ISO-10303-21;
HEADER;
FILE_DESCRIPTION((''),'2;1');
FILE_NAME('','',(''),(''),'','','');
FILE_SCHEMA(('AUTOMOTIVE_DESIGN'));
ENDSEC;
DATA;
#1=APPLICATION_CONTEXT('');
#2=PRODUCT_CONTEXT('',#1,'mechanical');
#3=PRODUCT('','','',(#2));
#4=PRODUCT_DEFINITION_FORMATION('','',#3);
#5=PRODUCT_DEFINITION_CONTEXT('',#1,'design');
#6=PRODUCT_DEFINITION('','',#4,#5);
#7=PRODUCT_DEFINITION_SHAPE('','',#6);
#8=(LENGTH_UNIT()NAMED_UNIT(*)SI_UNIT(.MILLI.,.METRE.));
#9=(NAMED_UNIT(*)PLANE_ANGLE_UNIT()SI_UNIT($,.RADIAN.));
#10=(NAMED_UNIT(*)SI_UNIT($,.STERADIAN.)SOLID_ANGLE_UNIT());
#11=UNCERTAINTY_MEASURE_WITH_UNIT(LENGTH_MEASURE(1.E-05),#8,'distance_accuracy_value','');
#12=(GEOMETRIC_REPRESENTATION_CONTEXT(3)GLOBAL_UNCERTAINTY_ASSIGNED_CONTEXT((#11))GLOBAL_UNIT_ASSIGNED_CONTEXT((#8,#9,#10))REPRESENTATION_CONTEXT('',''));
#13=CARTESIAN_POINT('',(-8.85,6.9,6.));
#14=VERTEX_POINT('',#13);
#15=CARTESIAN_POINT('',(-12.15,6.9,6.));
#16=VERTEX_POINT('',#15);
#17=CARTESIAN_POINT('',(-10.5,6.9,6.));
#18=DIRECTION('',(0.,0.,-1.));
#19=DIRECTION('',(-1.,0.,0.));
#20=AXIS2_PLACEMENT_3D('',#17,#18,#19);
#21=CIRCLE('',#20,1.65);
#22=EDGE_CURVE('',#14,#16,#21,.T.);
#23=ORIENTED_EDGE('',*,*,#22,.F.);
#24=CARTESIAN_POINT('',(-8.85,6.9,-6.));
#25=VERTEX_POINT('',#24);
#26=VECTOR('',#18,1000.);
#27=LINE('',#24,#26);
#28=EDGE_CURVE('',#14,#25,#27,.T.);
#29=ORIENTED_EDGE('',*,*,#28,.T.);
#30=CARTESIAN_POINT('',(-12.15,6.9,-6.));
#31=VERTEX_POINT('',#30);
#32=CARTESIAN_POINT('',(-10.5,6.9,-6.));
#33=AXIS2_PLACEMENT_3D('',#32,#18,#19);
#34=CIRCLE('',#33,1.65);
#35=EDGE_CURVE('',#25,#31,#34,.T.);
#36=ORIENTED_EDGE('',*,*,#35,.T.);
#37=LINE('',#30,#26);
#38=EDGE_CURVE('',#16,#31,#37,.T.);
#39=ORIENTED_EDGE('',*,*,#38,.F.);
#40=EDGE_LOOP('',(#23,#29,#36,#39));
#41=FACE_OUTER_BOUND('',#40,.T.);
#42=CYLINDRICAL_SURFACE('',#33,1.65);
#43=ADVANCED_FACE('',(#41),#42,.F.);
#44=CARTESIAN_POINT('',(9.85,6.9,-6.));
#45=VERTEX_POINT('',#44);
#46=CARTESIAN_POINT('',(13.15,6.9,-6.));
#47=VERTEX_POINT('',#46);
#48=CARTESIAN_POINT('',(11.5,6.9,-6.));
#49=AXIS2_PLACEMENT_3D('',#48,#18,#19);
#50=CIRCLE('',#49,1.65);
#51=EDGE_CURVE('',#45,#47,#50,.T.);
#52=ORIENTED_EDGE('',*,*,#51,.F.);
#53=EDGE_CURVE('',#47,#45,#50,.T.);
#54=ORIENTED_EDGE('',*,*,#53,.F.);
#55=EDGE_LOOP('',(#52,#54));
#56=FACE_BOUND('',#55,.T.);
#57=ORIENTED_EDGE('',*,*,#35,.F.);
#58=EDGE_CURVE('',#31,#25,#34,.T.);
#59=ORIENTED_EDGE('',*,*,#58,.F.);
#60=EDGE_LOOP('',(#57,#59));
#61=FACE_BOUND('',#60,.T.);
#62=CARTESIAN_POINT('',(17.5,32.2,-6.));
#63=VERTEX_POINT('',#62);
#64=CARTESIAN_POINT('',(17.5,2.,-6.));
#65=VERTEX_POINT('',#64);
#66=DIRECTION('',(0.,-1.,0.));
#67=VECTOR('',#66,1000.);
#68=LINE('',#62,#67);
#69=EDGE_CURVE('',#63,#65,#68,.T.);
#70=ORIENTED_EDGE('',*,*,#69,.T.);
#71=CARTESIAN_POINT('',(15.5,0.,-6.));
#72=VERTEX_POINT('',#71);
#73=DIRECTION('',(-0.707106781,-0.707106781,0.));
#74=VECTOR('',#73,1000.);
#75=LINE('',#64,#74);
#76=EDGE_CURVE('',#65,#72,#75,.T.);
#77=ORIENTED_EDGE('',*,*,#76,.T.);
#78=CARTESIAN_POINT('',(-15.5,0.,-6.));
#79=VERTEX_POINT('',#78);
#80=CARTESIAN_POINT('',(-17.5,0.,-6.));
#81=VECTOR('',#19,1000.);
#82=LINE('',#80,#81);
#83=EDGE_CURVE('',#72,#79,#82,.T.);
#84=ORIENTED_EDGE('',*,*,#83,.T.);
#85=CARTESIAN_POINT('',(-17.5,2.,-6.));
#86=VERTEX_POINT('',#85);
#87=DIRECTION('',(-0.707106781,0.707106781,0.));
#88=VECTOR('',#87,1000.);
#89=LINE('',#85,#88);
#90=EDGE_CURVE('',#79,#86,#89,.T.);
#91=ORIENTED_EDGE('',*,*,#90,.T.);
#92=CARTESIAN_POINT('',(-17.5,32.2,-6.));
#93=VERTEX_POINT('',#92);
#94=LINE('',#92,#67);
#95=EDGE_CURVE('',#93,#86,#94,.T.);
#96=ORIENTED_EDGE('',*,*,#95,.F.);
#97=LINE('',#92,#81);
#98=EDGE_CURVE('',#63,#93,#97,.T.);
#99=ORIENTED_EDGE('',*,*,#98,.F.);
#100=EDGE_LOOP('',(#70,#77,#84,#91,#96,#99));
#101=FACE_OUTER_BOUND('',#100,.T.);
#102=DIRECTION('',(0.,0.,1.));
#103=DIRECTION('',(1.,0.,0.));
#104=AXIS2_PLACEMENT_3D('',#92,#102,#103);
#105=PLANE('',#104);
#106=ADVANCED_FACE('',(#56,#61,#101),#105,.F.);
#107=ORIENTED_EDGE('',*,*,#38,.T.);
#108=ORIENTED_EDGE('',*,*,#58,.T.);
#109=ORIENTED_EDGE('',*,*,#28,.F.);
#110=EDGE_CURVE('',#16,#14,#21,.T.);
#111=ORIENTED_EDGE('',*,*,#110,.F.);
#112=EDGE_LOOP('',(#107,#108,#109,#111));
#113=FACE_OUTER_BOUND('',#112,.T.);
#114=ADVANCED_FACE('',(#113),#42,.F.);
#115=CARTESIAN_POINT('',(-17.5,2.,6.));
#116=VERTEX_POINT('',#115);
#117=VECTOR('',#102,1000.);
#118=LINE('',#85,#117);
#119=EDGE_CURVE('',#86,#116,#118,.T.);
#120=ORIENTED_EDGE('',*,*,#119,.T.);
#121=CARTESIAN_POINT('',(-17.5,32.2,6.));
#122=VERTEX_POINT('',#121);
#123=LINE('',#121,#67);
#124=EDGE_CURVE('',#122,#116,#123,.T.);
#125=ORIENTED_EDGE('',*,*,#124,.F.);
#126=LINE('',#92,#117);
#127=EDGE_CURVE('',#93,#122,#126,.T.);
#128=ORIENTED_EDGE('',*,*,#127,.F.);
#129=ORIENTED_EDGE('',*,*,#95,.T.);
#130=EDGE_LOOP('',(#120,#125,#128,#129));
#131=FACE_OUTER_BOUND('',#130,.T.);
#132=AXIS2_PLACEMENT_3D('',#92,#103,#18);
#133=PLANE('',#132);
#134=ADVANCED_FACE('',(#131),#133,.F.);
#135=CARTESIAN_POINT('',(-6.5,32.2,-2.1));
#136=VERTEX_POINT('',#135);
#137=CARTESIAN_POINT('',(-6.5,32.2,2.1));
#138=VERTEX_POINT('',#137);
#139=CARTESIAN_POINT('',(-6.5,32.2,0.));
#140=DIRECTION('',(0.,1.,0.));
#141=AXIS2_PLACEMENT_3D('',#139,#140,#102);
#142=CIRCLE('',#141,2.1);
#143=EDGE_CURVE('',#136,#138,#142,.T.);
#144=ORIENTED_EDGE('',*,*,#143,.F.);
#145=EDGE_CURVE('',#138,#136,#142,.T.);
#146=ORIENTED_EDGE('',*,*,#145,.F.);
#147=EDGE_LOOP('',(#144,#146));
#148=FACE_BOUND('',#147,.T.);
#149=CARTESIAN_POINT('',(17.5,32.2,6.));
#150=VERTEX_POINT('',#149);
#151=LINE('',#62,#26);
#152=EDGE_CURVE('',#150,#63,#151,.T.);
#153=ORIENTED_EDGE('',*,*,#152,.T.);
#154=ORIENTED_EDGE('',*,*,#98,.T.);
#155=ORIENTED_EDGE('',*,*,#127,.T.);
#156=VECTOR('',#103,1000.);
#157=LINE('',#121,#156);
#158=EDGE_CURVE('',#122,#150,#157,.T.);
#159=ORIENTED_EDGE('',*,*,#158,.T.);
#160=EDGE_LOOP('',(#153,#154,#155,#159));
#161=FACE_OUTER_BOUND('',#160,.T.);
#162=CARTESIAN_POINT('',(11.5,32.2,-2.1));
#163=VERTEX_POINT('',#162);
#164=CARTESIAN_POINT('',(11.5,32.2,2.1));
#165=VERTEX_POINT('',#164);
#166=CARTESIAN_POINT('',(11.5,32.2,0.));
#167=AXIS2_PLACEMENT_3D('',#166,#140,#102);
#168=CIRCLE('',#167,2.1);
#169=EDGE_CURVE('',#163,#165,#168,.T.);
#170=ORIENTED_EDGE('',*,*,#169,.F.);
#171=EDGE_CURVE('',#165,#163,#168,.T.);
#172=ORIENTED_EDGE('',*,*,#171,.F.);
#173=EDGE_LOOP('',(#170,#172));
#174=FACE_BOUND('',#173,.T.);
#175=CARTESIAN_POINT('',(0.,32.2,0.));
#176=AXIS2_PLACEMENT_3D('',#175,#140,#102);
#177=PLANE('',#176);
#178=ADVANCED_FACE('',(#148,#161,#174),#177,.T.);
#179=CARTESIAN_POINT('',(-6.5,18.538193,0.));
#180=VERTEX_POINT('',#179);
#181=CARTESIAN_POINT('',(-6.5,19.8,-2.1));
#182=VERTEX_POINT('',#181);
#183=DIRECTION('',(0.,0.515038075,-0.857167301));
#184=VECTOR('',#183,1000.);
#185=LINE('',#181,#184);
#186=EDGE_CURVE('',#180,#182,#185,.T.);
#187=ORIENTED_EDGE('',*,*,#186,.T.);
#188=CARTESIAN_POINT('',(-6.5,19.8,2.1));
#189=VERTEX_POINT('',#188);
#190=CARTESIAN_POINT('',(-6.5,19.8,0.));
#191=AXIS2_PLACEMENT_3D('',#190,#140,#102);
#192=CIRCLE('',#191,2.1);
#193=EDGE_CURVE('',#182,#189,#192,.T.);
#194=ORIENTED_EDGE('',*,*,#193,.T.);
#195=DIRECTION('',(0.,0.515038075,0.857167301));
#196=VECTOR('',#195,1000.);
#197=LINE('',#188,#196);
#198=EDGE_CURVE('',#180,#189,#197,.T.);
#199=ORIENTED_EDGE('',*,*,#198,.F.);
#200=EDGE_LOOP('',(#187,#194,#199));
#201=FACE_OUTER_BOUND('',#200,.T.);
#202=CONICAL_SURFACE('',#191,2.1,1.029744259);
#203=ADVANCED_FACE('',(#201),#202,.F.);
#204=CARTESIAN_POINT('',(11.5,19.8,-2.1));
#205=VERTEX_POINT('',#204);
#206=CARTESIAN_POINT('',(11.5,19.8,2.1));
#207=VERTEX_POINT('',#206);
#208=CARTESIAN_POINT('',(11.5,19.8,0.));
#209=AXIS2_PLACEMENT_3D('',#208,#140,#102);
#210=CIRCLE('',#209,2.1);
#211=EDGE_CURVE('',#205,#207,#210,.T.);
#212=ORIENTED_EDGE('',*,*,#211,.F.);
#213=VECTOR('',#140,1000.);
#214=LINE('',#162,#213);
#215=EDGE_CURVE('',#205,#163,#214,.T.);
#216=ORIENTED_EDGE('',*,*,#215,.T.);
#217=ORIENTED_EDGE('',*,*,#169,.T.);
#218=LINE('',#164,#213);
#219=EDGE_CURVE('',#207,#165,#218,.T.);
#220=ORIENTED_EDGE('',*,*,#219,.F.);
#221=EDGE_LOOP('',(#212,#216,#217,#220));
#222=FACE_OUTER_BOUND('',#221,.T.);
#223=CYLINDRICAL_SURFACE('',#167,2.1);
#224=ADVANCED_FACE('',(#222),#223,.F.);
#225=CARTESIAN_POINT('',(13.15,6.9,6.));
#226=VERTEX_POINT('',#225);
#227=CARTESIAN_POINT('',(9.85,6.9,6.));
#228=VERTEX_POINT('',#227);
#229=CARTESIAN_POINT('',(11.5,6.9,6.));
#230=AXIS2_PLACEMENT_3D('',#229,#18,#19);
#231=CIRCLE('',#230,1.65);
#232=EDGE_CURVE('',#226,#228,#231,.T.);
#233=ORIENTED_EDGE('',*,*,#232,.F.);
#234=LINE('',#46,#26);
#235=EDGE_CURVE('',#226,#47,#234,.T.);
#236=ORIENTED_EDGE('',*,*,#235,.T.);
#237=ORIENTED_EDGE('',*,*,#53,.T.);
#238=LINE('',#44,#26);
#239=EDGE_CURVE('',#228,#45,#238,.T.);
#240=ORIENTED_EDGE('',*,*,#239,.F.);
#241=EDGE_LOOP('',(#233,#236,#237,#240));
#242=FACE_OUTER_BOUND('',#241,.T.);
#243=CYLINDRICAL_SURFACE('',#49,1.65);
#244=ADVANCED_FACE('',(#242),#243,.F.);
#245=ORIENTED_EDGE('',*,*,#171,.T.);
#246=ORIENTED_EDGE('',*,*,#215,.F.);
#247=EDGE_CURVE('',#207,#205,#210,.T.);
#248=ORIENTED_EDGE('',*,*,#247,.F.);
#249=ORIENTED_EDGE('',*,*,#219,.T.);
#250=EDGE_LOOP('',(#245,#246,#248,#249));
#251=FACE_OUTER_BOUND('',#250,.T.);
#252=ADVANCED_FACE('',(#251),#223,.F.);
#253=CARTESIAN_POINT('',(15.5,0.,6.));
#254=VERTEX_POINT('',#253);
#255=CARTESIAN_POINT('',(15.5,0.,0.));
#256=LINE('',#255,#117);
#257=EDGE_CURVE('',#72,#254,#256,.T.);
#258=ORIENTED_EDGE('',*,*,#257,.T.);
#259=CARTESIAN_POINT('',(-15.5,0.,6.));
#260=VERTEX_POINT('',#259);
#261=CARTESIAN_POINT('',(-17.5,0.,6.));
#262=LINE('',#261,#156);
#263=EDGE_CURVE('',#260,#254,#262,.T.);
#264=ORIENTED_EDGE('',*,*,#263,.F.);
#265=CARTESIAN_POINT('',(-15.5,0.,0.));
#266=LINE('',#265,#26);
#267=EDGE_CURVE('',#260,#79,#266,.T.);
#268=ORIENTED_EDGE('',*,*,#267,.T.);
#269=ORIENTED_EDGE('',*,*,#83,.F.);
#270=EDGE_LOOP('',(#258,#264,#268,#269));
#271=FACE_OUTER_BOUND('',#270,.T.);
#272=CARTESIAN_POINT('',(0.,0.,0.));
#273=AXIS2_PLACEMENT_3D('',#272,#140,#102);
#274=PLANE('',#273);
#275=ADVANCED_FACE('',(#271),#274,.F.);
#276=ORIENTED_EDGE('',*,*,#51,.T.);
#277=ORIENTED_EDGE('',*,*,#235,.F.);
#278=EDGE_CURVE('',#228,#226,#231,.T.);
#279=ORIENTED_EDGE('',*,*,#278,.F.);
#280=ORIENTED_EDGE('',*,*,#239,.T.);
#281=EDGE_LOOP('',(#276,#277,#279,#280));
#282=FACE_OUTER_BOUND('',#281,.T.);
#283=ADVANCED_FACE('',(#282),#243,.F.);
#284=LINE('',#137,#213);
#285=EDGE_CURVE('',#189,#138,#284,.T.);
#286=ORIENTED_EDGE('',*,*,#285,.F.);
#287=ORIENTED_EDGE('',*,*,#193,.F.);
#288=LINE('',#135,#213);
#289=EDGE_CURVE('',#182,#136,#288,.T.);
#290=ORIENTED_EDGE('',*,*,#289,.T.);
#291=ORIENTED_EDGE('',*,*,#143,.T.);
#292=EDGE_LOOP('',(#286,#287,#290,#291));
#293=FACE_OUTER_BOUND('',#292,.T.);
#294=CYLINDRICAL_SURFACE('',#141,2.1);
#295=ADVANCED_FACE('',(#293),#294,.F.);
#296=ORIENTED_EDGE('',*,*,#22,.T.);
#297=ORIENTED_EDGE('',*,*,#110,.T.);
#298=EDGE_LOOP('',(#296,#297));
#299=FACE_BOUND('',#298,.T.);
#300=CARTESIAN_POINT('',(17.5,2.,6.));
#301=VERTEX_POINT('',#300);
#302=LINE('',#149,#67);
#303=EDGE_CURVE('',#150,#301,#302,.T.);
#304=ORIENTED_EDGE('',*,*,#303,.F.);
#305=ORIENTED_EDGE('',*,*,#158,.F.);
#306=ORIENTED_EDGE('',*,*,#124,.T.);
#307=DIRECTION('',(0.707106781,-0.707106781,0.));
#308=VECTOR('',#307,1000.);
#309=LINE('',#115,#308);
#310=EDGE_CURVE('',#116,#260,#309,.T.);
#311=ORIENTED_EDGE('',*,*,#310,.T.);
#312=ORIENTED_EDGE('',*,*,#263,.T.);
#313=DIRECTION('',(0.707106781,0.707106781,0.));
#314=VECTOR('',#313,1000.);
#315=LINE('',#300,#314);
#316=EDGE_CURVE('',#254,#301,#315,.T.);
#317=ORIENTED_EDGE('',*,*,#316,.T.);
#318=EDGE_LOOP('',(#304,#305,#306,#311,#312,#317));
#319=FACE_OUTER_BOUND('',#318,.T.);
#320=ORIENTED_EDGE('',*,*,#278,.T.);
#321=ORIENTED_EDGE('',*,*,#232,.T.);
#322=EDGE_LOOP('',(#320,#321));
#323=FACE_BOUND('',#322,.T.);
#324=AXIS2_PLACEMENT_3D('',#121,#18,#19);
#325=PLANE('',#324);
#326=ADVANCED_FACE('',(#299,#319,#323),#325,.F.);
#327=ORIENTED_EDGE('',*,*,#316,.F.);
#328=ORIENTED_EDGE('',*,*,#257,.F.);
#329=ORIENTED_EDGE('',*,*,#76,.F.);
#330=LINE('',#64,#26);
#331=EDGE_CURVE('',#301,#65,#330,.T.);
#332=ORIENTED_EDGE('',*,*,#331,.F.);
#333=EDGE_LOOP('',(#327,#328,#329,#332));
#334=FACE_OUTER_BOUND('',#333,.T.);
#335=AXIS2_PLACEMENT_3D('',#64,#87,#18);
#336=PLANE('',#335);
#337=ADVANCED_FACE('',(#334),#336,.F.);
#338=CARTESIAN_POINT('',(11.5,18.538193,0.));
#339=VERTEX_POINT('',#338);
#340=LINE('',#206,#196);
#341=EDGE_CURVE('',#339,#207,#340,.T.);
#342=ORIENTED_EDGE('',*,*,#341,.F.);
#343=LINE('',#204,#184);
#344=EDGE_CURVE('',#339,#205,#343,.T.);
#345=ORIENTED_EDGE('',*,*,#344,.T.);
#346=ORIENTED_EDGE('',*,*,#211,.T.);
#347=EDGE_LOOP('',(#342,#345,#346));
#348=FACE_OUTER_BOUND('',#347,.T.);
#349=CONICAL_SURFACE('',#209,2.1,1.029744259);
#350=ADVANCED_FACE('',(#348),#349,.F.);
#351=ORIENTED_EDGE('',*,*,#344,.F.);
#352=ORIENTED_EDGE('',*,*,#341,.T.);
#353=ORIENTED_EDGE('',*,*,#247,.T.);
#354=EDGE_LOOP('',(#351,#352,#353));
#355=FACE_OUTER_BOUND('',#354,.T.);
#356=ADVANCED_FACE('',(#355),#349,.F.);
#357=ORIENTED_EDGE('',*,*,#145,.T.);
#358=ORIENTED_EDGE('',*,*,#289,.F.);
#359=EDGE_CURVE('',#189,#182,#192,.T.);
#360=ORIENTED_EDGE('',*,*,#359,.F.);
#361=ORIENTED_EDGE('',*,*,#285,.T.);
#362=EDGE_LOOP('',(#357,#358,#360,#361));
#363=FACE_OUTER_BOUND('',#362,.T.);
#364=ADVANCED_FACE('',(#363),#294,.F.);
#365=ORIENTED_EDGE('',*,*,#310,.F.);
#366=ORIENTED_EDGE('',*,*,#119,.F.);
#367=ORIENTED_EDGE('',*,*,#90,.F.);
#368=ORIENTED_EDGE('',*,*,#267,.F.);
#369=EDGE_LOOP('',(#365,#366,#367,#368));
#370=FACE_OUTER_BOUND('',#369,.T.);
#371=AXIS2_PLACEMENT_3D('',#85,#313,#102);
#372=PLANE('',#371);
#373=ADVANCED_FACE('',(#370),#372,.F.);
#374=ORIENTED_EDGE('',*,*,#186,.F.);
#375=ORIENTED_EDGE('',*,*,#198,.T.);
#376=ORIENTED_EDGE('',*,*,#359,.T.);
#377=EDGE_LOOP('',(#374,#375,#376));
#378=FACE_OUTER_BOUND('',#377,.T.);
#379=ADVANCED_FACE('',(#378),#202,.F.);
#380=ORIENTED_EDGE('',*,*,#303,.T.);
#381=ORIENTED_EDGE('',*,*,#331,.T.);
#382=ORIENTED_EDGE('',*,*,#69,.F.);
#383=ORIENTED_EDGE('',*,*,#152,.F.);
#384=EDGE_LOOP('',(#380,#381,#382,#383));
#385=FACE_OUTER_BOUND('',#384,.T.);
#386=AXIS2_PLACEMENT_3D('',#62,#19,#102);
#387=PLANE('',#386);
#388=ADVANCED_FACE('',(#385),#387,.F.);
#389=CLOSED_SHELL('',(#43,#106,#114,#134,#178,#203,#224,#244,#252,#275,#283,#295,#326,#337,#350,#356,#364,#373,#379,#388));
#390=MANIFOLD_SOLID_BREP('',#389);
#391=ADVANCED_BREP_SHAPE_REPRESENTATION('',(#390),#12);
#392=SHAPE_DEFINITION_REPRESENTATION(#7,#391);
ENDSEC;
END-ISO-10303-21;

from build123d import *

# Parameters (mm, degrees)
SKETCH1_W             = 35
SKETCH1_H             = 12
BOSS_EXTRUDE1_DEPTH   = 32.2
M5_TAPPED_HOLE1_D     = 4.2
M5_TAPPED_HOLE1_DEPTH = 12.4
M5_TAPPED_HOLE1_TIP   = 1.2618073
CHAMFER2_SIZE         = 2
M4_TAPPED_HOLE1_D     = 3.3


with BuildPart() as part:
    # Sketch1 → Boss-Extrude1 (new body)
    with BuildSketch(Plane(origin=(0, 0, 0), x_dir=(1, 0, 0), z_dir=(0, 1, 0))):
        Rectangle(SKETCH1_W, SKETCH1_H)
    extrude(amount=BOSS_EXTRUDE1_DEPTH)

    # M5 Tapped Hole1
    with Locations(Plane(origin=(11.5, 32.2, 0), x_dir=(0, 0, 1), z_dir=(0, 1, 0))):
        with Locations((0, 0), (0, -18)):
            Hole(M5_TAPPED_HOLE1_D / 2, depth=M5_TAPPED_HOLE1_DEPTH)
            with Locations((0, 0, -(M5_TAPPED_HOLE1_DEPTH + M5_TAPPED_HOLE1_TIP / 2))):  # 118° drill point
                Cone(0, M5_TAPPED_HOLE1_D / 2, M5_TAPPED_HOLE1_TIP, mode=Mode.SUBTRACT)

    # Chamfer2
    chamfer2_edges = [part.edges().sort_by_distance(p)[0] for p in [
        (-17.5, 0, 0),
        (17.5, 0, 0),
    ]]
    chamfer(chamfer2_edges, length=CHAMFER2_SIZE)

    # M4 Tapped Hole1 (through all)
    with Locations(Plane(origin=(11.5, 6.9, -6), x_dir=(-1, 0, 0), z_dir=(0, 0, -1))):
        with Locations((0, 0), (22, 0)):
            Hole(M4_TAPPED_HOLE1_D / 2)


solid = part.part
